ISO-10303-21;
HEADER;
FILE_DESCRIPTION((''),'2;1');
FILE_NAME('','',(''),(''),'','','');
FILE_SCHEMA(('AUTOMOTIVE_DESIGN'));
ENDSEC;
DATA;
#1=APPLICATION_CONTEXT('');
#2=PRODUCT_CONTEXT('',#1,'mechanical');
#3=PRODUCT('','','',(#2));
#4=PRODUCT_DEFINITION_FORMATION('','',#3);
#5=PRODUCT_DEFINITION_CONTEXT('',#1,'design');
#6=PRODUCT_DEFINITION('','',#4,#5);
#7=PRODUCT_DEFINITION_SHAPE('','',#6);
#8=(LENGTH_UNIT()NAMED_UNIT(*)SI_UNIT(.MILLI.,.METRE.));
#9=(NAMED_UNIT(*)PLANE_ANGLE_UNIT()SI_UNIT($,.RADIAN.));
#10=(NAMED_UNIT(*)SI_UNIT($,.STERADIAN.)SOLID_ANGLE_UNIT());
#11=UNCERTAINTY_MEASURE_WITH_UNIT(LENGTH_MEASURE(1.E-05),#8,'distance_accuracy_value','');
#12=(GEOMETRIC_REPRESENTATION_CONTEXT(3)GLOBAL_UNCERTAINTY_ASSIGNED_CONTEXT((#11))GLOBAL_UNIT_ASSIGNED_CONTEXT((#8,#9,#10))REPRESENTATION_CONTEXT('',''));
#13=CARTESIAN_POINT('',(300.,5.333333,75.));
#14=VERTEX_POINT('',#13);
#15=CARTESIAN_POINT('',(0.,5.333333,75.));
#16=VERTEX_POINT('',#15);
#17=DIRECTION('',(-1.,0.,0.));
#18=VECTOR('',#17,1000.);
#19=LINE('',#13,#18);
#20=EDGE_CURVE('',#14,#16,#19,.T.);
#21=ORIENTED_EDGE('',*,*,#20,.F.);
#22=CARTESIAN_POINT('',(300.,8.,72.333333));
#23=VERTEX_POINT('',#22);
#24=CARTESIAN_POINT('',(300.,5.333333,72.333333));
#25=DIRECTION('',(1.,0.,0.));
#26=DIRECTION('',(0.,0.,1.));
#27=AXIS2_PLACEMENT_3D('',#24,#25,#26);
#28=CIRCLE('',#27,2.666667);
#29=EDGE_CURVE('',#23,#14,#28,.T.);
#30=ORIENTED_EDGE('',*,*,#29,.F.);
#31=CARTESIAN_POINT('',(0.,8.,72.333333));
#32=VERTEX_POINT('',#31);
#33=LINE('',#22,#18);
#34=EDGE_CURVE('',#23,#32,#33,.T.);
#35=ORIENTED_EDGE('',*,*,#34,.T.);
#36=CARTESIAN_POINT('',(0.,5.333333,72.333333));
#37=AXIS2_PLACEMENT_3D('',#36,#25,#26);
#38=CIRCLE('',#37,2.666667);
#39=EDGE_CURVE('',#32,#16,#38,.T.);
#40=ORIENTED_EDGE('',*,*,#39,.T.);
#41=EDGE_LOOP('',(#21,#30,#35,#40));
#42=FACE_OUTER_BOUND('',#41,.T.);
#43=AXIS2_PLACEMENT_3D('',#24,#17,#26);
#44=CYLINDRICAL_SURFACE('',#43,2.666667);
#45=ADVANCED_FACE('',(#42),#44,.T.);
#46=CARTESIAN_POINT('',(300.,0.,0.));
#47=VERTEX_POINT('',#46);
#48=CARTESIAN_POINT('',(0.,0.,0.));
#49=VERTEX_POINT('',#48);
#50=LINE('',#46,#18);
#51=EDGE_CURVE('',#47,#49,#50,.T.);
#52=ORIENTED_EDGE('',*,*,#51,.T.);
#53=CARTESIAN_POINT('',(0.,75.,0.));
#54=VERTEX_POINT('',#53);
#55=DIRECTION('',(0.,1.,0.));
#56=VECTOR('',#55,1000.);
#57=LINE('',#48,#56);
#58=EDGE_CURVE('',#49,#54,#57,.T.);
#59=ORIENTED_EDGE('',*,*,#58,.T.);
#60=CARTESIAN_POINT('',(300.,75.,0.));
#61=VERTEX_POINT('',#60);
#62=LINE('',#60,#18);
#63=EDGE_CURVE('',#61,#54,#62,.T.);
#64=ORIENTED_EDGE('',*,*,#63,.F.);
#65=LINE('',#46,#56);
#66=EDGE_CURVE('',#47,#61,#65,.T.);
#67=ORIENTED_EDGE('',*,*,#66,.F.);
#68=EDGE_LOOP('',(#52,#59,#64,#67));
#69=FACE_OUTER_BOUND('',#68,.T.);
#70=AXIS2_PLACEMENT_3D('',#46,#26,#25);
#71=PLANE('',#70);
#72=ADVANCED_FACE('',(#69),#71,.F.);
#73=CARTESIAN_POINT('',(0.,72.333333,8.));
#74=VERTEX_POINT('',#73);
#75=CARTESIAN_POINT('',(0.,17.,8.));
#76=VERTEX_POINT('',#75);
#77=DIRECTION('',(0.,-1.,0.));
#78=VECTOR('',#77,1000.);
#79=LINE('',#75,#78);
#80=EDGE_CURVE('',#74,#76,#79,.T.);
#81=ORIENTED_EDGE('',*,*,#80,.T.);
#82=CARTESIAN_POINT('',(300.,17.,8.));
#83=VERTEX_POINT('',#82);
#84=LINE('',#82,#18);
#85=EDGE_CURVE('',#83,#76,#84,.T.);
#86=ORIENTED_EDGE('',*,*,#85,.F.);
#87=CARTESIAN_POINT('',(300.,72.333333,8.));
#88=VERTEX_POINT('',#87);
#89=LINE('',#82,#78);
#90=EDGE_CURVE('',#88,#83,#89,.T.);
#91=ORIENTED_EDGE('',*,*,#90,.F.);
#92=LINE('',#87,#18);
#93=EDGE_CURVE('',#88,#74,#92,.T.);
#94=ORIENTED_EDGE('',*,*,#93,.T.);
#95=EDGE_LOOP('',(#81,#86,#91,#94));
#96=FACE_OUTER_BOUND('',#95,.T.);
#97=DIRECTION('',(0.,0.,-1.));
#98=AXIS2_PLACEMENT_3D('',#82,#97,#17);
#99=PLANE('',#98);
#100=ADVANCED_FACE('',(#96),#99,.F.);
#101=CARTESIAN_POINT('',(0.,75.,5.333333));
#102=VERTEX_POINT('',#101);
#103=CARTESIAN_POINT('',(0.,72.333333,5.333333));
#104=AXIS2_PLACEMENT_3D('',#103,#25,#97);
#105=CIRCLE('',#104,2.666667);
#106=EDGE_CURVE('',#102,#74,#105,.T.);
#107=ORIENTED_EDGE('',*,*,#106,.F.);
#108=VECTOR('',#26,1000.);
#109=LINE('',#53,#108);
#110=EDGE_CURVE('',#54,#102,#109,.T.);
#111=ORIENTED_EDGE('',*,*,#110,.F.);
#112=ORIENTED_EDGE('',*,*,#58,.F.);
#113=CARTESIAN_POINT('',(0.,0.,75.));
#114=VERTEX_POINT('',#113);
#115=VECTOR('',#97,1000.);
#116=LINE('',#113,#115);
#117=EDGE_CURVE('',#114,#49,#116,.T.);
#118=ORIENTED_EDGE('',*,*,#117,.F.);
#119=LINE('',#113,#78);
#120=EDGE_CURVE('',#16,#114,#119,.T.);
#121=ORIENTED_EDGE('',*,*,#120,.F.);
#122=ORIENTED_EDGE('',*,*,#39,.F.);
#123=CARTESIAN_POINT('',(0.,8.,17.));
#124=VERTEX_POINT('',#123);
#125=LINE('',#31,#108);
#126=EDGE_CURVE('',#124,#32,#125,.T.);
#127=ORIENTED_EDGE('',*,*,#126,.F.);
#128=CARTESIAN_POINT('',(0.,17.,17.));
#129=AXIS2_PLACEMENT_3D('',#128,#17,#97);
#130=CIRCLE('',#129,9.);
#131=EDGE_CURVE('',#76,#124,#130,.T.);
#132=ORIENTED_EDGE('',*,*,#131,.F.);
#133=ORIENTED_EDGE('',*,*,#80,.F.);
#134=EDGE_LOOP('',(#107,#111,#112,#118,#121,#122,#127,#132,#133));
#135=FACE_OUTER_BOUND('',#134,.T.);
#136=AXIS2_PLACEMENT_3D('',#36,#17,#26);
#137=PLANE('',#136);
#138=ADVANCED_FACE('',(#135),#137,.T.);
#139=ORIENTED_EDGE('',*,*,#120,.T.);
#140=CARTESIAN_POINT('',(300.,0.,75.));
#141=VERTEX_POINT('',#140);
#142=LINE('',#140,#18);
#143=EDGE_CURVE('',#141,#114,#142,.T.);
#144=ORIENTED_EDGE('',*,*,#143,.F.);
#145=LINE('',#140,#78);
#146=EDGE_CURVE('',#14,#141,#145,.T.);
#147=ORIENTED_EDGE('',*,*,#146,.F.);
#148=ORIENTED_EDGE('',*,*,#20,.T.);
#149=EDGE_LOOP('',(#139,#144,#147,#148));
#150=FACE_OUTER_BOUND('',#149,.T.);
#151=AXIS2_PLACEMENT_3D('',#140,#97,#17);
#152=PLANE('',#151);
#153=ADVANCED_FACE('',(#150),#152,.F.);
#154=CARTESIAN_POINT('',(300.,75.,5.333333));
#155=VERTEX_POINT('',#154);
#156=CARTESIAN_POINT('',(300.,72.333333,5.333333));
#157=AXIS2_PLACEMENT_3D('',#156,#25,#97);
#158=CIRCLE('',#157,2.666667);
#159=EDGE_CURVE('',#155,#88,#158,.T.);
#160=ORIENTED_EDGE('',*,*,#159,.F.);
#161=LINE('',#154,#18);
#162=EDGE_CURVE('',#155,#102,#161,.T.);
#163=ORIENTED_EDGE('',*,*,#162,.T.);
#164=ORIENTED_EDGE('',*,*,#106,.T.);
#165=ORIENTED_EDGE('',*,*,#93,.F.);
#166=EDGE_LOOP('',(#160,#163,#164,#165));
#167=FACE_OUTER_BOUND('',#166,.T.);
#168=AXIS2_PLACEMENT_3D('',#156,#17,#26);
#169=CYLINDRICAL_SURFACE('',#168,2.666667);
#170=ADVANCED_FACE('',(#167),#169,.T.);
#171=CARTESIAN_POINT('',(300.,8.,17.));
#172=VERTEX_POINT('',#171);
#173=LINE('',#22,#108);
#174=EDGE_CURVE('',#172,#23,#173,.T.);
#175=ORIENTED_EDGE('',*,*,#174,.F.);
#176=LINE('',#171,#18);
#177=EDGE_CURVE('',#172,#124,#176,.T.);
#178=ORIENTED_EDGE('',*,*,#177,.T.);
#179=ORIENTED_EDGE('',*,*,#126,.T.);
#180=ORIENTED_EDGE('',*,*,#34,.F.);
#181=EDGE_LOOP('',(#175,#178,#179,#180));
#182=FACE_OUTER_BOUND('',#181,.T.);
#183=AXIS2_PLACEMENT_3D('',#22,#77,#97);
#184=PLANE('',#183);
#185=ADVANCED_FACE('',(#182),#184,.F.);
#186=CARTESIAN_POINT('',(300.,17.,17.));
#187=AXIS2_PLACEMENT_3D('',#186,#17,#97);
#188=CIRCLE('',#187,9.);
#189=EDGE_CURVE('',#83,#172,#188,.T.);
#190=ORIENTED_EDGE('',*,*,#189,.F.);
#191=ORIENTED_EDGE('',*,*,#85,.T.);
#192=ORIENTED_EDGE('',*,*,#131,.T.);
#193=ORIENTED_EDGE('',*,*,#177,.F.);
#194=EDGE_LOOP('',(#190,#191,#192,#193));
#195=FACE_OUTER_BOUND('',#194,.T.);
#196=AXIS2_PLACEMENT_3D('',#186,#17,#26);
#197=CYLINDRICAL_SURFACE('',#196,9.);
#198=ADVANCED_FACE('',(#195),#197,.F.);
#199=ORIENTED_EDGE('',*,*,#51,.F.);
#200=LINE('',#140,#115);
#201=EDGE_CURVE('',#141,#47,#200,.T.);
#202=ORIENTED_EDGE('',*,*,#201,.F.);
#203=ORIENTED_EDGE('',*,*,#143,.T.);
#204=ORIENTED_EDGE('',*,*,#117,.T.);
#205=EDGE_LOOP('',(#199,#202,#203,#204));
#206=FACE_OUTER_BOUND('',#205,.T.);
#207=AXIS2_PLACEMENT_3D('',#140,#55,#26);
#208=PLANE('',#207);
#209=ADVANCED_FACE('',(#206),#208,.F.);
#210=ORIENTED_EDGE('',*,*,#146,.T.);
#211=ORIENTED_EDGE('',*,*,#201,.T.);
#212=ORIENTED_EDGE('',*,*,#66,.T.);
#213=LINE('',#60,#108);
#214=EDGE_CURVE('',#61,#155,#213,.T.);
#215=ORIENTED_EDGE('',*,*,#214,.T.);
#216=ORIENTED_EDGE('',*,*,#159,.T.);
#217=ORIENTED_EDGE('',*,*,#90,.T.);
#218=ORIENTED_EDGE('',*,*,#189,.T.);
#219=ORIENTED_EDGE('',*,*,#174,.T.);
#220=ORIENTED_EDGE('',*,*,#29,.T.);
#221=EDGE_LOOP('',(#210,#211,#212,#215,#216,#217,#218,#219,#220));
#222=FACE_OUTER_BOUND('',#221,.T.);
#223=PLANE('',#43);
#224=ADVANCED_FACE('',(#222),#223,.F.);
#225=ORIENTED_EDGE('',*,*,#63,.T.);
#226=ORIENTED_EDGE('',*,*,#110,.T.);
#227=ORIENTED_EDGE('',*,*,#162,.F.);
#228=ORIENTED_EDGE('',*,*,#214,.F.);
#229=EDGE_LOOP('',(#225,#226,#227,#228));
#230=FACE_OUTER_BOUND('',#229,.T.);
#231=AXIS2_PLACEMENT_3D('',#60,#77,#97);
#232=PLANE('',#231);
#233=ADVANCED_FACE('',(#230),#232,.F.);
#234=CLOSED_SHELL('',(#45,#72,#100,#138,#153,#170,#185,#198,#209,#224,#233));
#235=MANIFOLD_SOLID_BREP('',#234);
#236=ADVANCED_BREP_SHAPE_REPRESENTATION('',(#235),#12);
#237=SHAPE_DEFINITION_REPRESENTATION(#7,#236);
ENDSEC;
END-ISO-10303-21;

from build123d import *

# Parameters (mm, degrees)
BASE_DEPTH = 300


with BuildPart() as part:
    # Sketch1 → Base (new body)
    with BuildSketch(Plane.YZ):
        with BuildLine():
            Line((0, 75), (0, 0))
            Line((0, 0), (75, 0))
            Line((75, 0), (75, 5.333333333))
            ThreePointArc((75, 5.333333333), (74.218951416, 7.218951416), (72.333333333, 8))
            Line((72.333333333, 8), (17, 8))
            ThreePointArc((17, 8), (10.636038969, 10.636038969), (8, 17))
            Line((8, 17), (8, 72.333333333))
            ThreePointArc((8, 72.333333333), (7.218951416, 74.218951416), (5.333333333, 75))
            Line((5.333333333, 75), (0, 75))
        make_face()
    extrude(amount=BASE_DEPTH)


solid = part.part
